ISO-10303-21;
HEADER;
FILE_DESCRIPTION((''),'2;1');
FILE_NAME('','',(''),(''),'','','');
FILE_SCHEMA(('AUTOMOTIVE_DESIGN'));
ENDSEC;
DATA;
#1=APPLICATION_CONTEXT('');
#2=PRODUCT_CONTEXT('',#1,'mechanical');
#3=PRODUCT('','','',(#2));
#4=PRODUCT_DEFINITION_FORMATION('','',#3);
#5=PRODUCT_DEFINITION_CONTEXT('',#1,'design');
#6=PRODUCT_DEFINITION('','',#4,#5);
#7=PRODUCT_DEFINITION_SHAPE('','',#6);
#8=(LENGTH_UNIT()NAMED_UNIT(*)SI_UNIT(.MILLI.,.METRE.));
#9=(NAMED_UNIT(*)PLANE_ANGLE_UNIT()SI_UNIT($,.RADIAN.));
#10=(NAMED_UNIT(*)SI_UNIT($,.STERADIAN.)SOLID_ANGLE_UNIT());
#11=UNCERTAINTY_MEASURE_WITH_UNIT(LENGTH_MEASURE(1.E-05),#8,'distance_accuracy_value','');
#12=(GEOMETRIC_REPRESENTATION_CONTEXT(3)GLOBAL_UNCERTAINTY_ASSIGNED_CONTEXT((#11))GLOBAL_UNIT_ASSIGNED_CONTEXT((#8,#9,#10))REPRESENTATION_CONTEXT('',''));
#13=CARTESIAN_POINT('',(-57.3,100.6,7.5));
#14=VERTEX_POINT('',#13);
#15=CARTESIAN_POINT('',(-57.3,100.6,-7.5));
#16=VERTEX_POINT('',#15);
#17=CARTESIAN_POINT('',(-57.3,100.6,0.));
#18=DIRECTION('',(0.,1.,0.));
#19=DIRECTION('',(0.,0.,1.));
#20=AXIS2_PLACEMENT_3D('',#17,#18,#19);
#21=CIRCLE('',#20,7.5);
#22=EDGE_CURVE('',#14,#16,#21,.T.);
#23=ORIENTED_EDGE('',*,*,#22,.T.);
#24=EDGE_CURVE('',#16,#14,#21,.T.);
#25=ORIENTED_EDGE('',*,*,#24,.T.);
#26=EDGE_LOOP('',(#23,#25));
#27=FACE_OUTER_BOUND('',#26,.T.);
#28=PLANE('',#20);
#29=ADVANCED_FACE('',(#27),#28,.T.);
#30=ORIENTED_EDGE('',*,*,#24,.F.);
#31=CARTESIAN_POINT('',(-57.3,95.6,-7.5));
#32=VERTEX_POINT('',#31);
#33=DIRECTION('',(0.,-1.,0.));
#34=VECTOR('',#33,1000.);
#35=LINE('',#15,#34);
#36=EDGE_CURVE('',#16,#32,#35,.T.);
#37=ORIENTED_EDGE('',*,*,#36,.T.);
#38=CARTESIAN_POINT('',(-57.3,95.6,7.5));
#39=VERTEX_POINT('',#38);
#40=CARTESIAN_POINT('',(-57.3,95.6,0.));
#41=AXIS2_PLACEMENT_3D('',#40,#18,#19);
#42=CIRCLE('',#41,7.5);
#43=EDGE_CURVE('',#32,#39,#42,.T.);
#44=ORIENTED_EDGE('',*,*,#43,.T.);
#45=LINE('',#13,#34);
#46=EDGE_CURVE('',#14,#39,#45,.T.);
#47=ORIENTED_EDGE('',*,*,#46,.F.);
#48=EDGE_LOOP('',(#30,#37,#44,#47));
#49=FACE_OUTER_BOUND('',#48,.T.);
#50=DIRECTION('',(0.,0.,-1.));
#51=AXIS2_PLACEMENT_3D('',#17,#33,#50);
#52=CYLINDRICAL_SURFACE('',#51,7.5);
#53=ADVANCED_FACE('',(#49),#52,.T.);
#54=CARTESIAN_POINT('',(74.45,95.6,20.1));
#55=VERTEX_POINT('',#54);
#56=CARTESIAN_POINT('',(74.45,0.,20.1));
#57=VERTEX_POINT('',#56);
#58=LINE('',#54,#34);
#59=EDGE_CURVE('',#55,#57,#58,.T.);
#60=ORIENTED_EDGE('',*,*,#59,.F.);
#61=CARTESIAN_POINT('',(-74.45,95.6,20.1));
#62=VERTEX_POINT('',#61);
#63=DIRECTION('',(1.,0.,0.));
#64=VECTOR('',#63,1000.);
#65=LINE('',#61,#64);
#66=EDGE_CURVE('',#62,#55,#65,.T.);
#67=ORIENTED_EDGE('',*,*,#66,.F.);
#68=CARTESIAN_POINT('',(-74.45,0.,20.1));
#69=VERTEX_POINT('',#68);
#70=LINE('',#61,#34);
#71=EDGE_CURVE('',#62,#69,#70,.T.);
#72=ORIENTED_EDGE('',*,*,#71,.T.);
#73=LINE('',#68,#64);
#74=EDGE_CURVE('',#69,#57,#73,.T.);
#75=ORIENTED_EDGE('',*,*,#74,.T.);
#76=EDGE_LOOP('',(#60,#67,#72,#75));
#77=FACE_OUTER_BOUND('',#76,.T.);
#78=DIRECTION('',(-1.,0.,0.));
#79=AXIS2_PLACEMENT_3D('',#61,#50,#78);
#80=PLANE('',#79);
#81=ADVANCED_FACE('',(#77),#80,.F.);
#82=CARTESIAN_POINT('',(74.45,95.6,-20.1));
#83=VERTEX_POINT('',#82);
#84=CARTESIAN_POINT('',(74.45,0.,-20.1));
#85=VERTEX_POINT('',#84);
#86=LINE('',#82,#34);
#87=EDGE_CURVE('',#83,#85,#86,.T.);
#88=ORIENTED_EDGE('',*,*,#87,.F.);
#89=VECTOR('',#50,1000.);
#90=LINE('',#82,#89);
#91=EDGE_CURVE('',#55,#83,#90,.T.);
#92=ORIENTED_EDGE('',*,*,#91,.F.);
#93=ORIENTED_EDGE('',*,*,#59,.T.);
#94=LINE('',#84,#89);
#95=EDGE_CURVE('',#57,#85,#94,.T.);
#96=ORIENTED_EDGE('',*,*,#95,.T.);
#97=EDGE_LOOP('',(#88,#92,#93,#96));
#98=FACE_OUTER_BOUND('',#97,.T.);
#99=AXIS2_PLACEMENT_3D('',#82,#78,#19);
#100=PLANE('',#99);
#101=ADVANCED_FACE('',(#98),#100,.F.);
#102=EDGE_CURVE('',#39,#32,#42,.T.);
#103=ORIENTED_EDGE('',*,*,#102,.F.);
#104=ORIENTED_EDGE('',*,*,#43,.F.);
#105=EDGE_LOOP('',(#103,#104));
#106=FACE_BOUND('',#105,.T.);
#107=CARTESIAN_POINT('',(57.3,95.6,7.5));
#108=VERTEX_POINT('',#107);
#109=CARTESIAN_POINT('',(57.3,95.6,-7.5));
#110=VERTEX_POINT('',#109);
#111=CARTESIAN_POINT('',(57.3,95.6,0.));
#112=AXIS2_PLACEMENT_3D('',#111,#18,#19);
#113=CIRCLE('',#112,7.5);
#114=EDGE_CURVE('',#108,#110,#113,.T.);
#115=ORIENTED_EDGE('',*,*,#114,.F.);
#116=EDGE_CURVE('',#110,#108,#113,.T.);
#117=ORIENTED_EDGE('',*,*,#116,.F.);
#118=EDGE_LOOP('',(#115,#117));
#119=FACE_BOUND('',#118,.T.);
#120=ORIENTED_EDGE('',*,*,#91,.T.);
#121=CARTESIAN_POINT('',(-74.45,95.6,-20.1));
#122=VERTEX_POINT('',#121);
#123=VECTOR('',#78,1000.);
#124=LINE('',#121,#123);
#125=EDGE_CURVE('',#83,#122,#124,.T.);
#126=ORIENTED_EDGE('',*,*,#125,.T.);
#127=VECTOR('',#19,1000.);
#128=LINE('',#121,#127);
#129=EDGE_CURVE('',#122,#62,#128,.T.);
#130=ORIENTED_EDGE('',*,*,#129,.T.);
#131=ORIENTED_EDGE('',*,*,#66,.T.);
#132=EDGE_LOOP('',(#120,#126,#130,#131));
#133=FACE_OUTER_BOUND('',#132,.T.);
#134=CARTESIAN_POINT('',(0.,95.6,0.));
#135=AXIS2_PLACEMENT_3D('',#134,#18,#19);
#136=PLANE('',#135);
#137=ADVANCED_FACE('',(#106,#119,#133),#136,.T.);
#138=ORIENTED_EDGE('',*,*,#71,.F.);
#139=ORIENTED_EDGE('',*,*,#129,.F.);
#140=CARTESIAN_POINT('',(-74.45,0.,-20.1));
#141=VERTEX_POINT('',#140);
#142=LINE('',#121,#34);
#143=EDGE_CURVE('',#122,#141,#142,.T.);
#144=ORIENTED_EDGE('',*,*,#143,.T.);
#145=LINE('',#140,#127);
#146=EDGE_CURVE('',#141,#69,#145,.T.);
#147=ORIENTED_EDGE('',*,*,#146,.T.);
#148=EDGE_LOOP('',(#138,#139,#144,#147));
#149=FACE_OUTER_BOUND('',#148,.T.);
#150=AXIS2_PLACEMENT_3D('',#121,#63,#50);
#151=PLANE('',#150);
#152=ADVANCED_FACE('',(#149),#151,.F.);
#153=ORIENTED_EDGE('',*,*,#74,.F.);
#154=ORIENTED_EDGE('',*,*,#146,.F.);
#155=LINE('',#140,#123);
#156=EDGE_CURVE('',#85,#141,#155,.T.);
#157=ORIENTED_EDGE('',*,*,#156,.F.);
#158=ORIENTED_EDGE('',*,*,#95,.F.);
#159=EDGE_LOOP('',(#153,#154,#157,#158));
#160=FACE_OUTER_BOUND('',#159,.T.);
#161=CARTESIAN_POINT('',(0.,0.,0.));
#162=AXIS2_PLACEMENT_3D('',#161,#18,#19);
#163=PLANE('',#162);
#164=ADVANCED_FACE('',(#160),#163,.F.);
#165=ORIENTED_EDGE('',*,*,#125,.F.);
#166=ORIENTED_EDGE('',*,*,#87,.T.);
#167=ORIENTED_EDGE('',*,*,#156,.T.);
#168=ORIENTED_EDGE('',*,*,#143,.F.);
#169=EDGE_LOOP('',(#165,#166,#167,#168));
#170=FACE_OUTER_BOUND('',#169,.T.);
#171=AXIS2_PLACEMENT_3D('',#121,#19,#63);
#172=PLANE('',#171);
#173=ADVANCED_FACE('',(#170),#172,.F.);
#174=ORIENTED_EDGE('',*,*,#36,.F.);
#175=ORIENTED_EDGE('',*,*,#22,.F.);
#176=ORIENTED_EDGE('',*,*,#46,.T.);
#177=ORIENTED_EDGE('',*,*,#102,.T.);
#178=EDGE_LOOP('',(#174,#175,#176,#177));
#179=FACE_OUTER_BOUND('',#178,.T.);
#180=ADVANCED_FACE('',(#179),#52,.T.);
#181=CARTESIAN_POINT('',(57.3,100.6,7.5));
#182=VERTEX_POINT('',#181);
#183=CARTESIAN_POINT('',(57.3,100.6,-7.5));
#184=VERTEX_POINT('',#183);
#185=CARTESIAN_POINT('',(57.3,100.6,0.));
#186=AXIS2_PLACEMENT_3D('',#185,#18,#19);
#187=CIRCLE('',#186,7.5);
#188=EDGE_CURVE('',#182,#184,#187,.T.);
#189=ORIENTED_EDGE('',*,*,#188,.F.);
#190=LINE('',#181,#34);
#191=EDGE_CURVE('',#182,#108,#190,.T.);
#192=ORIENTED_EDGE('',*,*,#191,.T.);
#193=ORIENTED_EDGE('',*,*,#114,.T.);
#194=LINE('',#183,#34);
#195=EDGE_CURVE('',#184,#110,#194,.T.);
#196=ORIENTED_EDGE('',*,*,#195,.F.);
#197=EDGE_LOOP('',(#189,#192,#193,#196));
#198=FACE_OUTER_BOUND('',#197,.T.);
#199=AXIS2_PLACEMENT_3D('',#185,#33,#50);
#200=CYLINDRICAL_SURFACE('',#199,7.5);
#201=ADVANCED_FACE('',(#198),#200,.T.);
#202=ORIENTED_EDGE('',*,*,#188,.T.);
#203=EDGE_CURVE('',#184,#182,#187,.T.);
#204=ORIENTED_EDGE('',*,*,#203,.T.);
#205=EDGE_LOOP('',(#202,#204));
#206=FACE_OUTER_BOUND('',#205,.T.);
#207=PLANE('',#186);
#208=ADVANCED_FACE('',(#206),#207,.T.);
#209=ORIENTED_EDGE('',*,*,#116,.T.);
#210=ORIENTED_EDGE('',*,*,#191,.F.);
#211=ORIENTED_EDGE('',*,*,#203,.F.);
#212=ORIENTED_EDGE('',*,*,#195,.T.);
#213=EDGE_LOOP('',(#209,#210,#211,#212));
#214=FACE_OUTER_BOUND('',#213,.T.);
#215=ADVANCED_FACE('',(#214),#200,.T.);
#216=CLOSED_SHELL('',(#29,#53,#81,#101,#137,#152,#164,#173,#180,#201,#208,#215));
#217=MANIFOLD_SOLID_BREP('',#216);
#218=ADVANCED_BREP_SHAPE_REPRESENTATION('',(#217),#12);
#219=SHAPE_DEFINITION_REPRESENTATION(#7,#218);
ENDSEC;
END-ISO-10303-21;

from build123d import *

# Parameters (mm, degrees)
SKETCH_1_W      = 148.9
SKETCH_1_H      = 40.2
EXTRUDE_1_DEPTH = 95.6
SKETCH_2_R      = 7.5
EXTRUDE_2_DEPTH = 5


with BuildPart() as part:
    # 草图1 → 凸台-拉伸1 (new body)
    with BuildSketch(Plane(origin=(0, 0, 0), x_dir=(1, 0, 0), z_dir=(0, 1, 0))):
        Rectangle(SKETCH_1_W, SKETCH_1_H)
    extrude(amount=EXTRUDE_1_DEPTH)

    # 草图2 → 凸台-拉伸2 (add)
    with BuildSketch(Plane(origin=(0, 95.6, 0), x_dir=(1, 0, 0), z_dir=(0, 1, 0))):
        with Locations(Location((57.3, 0, 0), (0, 0, 270))):
            Circle(SKETCH_2_R)
        with Locations(Location((-57.3, 0, 0), (0, 0, 270))):
            Circle(SKETCH_2_R)
    extrude(amount=EXTRUDE_2_DEPTH)


solid = part.part
